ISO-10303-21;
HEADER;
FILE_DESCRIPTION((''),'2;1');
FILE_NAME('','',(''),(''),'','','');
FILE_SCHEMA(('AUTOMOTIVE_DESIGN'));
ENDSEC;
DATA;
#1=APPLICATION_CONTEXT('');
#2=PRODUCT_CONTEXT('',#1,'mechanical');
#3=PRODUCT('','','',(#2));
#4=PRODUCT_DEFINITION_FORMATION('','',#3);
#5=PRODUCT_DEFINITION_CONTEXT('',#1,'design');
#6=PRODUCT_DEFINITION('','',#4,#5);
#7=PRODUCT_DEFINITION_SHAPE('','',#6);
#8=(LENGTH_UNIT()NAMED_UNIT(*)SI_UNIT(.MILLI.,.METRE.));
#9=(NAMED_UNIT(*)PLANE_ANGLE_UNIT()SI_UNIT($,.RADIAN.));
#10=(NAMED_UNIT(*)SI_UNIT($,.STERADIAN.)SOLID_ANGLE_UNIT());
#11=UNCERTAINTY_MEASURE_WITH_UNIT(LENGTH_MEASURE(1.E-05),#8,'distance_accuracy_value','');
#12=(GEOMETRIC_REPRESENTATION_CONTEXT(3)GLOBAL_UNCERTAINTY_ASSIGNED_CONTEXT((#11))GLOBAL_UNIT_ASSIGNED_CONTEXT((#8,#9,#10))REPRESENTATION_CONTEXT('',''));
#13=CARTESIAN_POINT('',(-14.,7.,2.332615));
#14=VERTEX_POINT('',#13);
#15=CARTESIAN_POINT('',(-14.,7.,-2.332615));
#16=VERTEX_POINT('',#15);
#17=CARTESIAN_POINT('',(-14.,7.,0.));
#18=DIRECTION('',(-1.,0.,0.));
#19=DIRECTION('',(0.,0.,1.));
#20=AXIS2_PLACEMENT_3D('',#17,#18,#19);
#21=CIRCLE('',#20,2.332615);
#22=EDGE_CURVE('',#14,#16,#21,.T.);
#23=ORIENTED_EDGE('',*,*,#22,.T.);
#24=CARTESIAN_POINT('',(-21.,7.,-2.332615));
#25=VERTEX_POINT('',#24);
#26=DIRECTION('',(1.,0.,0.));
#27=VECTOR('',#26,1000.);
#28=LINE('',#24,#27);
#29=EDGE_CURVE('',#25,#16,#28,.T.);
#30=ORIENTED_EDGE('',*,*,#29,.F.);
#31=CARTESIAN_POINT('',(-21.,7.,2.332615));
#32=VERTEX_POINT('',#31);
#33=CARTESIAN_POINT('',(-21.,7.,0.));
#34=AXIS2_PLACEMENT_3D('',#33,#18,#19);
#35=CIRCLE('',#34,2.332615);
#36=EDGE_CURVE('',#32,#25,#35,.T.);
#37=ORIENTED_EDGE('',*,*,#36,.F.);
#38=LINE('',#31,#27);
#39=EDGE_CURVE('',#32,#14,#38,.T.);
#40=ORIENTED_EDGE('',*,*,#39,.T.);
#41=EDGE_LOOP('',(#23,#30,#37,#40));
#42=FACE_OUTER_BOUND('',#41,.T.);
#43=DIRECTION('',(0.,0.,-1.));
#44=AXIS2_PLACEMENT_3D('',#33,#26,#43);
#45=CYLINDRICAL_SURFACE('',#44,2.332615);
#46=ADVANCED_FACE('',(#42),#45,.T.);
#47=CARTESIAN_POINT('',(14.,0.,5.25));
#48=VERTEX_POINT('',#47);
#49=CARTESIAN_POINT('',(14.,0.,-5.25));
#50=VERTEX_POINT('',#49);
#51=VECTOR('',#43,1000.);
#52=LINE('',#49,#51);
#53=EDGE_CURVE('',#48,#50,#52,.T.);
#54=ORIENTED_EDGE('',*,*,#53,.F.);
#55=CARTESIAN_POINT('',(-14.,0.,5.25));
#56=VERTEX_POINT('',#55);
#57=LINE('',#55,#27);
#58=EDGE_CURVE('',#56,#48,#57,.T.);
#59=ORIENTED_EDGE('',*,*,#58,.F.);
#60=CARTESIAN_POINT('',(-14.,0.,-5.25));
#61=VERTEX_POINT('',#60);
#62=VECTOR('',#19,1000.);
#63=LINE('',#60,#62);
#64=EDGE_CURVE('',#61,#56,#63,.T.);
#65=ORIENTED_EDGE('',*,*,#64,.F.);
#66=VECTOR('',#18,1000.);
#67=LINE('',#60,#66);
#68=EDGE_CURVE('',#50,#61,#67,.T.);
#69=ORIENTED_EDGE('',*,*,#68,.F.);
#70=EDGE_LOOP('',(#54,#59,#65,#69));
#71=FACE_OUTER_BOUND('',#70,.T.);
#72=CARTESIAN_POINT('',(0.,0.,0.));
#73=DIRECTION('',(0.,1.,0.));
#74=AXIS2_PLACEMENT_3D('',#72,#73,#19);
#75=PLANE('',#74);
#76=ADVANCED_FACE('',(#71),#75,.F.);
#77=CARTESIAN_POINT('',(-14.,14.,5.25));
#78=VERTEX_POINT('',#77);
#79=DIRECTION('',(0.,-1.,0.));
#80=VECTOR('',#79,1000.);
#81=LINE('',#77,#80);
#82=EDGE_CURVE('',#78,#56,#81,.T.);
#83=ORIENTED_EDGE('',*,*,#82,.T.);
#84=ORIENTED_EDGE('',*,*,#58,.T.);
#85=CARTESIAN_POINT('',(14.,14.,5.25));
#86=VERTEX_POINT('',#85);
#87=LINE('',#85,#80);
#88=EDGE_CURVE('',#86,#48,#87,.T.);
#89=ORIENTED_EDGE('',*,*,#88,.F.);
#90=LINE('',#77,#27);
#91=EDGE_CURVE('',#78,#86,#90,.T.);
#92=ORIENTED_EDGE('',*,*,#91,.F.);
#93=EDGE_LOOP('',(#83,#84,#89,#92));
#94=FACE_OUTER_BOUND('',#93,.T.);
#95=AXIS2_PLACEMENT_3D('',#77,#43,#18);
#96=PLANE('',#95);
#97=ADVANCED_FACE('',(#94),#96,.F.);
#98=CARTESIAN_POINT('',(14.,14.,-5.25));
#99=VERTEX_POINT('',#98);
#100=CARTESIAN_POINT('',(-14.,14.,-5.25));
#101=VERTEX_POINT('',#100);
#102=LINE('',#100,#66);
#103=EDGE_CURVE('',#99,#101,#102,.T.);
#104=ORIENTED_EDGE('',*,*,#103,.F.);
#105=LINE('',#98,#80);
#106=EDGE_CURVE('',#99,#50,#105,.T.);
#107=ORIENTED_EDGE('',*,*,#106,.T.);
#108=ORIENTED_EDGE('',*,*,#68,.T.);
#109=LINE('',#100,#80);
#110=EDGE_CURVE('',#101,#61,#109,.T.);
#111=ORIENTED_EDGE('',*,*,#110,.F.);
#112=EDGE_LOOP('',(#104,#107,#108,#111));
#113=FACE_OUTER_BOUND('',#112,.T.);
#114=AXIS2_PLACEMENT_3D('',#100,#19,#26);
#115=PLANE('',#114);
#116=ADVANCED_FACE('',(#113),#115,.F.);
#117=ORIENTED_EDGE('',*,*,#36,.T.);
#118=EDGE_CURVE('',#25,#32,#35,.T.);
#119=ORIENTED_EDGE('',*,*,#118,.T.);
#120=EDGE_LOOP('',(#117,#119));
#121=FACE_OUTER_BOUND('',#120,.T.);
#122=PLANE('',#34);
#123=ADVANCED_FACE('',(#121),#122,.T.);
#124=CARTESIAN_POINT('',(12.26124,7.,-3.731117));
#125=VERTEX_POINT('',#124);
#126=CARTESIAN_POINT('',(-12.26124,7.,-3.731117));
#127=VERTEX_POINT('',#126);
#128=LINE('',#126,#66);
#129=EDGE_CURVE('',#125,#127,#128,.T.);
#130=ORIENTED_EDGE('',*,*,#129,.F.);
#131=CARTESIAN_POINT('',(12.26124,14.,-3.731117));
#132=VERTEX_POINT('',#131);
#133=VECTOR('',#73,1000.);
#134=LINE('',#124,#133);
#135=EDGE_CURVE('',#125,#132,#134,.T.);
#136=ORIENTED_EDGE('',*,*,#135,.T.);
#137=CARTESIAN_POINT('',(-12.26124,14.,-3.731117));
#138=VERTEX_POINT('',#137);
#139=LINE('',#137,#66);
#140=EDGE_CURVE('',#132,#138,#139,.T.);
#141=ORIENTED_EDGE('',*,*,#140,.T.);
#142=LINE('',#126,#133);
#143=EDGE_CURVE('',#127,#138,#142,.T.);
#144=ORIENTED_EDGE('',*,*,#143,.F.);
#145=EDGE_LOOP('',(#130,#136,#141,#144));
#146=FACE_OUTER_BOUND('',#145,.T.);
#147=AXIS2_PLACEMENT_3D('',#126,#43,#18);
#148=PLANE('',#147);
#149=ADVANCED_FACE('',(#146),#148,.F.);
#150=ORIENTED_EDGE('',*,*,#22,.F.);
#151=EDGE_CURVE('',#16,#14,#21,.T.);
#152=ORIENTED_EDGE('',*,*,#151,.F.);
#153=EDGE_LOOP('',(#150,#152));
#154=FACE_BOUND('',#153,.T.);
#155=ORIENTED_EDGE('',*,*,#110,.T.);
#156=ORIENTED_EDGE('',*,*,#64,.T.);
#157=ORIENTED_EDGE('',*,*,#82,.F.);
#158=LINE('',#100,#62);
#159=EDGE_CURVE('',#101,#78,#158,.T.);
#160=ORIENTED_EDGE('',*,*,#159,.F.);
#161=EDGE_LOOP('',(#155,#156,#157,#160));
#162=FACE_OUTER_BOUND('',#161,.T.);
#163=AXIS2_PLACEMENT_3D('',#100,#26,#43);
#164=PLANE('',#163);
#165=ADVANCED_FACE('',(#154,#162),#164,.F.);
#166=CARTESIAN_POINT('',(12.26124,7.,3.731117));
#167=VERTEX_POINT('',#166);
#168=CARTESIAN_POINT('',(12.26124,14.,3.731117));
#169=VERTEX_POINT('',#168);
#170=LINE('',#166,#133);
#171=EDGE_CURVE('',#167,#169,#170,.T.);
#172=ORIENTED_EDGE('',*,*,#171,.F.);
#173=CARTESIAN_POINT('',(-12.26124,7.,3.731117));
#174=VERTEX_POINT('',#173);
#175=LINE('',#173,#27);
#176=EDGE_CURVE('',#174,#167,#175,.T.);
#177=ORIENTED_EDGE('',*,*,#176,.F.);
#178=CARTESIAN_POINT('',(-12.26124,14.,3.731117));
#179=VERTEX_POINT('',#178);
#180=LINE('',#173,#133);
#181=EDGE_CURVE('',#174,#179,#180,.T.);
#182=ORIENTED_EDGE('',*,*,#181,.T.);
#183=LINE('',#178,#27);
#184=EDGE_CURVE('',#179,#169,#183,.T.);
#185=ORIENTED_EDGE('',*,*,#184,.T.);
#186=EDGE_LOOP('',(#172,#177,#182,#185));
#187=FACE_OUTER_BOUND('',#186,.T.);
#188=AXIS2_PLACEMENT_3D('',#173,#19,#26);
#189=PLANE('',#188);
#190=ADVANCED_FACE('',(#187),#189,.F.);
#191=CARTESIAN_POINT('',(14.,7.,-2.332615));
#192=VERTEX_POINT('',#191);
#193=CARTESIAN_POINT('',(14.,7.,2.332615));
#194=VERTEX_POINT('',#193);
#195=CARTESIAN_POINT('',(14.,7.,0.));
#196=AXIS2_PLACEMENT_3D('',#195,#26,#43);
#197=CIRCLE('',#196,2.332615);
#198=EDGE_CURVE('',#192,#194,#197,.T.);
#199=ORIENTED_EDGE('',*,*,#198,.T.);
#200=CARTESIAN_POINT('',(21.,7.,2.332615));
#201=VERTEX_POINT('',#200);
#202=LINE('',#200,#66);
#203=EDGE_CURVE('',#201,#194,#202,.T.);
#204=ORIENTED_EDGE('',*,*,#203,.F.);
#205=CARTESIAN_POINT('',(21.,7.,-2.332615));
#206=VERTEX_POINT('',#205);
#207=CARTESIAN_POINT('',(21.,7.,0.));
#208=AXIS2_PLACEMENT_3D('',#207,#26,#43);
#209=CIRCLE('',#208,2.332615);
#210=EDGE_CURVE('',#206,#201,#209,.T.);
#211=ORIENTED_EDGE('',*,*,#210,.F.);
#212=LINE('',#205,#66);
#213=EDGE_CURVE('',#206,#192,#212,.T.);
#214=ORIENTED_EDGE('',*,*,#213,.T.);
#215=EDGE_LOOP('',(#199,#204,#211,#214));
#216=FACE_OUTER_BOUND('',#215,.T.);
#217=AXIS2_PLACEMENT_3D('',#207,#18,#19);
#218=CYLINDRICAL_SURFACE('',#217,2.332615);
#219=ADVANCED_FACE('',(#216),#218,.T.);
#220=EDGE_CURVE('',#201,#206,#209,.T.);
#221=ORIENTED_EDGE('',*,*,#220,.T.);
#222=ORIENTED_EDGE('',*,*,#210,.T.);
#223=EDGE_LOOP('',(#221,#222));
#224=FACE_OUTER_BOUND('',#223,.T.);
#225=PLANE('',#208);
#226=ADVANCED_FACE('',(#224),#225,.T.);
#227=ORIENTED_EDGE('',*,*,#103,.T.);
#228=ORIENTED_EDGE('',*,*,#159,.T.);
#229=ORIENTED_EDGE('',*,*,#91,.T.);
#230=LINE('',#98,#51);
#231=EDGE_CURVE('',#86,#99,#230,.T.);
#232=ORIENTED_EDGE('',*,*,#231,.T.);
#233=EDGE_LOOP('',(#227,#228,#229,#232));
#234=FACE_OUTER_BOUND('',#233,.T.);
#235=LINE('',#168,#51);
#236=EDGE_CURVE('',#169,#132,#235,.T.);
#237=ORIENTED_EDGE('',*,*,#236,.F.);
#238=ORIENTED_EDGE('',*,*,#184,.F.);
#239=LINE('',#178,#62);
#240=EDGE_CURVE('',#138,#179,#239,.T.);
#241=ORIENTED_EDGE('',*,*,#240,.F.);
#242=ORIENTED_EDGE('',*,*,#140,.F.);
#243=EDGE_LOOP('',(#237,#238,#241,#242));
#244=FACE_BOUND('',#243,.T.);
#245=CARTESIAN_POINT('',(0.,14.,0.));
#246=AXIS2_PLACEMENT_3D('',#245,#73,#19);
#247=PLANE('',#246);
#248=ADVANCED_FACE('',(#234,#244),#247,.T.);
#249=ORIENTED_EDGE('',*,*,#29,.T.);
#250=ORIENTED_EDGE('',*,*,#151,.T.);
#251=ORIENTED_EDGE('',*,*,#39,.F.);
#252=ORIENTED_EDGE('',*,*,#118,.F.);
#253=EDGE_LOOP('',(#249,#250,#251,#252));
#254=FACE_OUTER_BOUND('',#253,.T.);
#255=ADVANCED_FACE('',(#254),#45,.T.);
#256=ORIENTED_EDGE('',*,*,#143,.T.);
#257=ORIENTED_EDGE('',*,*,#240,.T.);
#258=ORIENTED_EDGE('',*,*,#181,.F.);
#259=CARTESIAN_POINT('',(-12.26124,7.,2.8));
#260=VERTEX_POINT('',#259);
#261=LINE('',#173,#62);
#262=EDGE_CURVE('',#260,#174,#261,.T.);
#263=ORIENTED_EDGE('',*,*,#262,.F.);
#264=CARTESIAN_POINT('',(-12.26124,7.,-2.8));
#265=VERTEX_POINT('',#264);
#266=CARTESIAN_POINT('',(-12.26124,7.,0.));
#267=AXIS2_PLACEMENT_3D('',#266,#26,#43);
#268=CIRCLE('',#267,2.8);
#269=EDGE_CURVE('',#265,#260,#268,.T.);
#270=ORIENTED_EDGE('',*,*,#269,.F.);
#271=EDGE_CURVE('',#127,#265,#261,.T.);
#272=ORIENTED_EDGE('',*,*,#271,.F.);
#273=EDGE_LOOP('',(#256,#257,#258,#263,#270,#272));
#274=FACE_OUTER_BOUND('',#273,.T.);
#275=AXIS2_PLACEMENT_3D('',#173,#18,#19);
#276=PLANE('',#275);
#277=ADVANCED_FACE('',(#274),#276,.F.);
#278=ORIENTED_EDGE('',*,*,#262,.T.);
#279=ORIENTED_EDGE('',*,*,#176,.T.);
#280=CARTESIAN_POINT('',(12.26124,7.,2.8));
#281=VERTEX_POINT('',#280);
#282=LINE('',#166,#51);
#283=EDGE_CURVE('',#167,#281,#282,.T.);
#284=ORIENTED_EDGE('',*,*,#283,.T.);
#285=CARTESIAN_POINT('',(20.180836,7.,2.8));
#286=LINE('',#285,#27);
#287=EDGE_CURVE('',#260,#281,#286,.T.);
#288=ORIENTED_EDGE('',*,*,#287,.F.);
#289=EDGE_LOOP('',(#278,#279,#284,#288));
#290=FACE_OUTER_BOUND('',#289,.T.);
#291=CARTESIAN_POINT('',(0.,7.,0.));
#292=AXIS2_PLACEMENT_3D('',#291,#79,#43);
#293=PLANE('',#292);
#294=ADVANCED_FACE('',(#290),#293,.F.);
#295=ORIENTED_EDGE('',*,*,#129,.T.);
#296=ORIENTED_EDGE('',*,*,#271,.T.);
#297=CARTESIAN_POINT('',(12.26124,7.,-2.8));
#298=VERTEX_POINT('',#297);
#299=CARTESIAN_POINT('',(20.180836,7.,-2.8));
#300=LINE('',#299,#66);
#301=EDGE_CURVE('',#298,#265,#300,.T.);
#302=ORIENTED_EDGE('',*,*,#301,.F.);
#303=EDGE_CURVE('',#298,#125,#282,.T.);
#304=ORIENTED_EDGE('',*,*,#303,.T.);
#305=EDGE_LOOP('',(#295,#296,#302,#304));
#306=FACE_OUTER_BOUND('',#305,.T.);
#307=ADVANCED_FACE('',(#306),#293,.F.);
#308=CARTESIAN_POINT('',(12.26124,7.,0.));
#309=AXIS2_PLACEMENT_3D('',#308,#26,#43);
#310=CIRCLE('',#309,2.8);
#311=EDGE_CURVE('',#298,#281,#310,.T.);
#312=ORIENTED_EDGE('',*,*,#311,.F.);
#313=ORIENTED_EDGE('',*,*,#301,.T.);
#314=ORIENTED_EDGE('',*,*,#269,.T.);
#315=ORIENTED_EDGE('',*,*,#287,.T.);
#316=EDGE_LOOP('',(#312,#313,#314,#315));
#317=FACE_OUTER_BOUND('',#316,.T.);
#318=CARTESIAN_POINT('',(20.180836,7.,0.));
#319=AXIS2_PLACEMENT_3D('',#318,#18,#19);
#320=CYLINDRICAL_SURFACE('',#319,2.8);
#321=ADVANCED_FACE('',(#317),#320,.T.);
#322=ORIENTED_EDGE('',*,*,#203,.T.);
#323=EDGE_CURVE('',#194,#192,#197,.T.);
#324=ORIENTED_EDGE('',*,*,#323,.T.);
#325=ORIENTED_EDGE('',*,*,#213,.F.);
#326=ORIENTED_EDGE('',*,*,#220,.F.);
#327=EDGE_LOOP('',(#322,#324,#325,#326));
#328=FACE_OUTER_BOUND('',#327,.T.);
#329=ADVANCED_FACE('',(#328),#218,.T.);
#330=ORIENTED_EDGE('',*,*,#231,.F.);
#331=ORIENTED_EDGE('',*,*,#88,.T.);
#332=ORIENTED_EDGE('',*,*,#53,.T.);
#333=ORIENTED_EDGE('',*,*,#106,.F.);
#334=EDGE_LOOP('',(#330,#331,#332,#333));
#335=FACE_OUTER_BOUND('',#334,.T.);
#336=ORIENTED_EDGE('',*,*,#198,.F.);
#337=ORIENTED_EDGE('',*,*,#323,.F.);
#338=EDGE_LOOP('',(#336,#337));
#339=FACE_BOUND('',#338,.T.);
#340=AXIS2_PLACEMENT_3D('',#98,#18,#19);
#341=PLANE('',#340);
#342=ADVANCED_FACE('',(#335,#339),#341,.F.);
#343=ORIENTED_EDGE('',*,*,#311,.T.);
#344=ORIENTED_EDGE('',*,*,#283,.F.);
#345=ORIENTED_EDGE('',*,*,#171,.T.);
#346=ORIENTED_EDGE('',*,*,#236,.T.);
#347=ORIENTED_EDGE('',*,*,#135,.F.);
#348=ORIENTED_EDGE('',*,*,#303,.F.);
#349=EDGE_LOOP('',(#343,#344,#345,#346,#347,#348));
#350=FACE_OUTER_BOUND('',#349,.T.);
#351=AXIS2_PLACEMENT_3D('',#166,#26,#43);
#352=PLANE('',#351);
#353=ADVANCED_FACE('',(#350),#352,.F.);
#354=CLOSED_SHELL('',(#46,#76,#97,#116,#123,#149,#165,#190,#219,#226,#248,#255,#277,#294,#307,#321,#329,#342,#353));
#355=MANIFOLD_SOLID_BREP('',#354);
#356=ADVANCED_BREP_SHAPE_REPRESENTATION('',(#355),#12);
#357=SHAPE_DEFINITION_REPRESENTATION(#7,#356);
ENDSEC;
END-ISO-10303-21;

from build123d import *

# Parameters (mm, degrees)
SKETCH1_W           = 40
SKETCH1_H           = 15
BOSS_EXTRUDE1_DEPTH = 20
SKETCH2_W           = 35.032113562
SKETCH2_H           = 10.660333008
CUT_EXTRUDE1_DEPTH  = 10
SKETCH3_R           = 4
BOSS_EXTRUDE2_DEPTH = 35.032113562
SKETCH4_R           = 3.332307017
BOSS_EXTRUDE3_DEPTH = 10
BOSS_EXTRUDE4_START = 10
SKETCH5_R           = 3.332307017
BOSS_EXTRUDE4_DEPTH = 10
SCALE1_SCALE        = 0.7


with BuildPart() as part:
    # Sketch1 → Boss-Extrude1 (new body)
    with BuildSketch(Plane(origin=(0, 0, 0), x_dir=(1, 0, 0), z_dir=(0, 1, 0))):
        Rectangle(SKETCH1_W, SKETCH1_H)
    extrude(amount=BOSS_EXTRUDE1_DEPTH)

    # Sketch2 → Cut-Extrude1 (cut)
    with BuildSketch(Plane(origin=(0, 20, 0), x_dir=(1, 0, 0), z_dir=(0, 1, 0))):
        Rectangle(SKETCH2_W, SKETCH2_H)
    extrude(amount=-CUT_EXTRUDE1_DEPTH, mode=Mode.SUBTRACT)

    # Sketch3 → Boss-Extrude2 (add)
    with BuildSketch(Plane(origin=(-17.516056781, 0, 0), x_dir=(0, 0, -1), z_dir=(1, 0, 0))):
        with Locations((0, 10)):
            Circle(SKETCH3_R)
    extrude(amount=BOSS_EXTRUDE2_DEPTH)

    # Sketch4 → Boss-Extrude3 (add)
    with BuildSketch(Plane.ZY.offset(20)):
        with Locations((0, 10)):
            Circle(SKETCH4_R)
    extrude(amount=BOSS_EXTRUDE3_DEPTH)

    # Sketch5 → Boss-Extrude4 (add)
    with BuildSketch(Plane(origin=(20, 0, 0), x_dir=(0, 0, -1), z_dir=(1, 0, 0)).offset(BOSS_EXTRUDE4_START)):
        with Locations(Location((0, 10, 0), (0, 0, 180))):
            Circle(SKETCH5_R)
    extrude(amount=-BOSS_EXTRUDE4_DEPTH)


with BuildPart() as part_1:
    # Scale1: scaled about (0, 0, 0)
    add(part.part.scale(SCALE1_SCALE))


solid = part_1.part
